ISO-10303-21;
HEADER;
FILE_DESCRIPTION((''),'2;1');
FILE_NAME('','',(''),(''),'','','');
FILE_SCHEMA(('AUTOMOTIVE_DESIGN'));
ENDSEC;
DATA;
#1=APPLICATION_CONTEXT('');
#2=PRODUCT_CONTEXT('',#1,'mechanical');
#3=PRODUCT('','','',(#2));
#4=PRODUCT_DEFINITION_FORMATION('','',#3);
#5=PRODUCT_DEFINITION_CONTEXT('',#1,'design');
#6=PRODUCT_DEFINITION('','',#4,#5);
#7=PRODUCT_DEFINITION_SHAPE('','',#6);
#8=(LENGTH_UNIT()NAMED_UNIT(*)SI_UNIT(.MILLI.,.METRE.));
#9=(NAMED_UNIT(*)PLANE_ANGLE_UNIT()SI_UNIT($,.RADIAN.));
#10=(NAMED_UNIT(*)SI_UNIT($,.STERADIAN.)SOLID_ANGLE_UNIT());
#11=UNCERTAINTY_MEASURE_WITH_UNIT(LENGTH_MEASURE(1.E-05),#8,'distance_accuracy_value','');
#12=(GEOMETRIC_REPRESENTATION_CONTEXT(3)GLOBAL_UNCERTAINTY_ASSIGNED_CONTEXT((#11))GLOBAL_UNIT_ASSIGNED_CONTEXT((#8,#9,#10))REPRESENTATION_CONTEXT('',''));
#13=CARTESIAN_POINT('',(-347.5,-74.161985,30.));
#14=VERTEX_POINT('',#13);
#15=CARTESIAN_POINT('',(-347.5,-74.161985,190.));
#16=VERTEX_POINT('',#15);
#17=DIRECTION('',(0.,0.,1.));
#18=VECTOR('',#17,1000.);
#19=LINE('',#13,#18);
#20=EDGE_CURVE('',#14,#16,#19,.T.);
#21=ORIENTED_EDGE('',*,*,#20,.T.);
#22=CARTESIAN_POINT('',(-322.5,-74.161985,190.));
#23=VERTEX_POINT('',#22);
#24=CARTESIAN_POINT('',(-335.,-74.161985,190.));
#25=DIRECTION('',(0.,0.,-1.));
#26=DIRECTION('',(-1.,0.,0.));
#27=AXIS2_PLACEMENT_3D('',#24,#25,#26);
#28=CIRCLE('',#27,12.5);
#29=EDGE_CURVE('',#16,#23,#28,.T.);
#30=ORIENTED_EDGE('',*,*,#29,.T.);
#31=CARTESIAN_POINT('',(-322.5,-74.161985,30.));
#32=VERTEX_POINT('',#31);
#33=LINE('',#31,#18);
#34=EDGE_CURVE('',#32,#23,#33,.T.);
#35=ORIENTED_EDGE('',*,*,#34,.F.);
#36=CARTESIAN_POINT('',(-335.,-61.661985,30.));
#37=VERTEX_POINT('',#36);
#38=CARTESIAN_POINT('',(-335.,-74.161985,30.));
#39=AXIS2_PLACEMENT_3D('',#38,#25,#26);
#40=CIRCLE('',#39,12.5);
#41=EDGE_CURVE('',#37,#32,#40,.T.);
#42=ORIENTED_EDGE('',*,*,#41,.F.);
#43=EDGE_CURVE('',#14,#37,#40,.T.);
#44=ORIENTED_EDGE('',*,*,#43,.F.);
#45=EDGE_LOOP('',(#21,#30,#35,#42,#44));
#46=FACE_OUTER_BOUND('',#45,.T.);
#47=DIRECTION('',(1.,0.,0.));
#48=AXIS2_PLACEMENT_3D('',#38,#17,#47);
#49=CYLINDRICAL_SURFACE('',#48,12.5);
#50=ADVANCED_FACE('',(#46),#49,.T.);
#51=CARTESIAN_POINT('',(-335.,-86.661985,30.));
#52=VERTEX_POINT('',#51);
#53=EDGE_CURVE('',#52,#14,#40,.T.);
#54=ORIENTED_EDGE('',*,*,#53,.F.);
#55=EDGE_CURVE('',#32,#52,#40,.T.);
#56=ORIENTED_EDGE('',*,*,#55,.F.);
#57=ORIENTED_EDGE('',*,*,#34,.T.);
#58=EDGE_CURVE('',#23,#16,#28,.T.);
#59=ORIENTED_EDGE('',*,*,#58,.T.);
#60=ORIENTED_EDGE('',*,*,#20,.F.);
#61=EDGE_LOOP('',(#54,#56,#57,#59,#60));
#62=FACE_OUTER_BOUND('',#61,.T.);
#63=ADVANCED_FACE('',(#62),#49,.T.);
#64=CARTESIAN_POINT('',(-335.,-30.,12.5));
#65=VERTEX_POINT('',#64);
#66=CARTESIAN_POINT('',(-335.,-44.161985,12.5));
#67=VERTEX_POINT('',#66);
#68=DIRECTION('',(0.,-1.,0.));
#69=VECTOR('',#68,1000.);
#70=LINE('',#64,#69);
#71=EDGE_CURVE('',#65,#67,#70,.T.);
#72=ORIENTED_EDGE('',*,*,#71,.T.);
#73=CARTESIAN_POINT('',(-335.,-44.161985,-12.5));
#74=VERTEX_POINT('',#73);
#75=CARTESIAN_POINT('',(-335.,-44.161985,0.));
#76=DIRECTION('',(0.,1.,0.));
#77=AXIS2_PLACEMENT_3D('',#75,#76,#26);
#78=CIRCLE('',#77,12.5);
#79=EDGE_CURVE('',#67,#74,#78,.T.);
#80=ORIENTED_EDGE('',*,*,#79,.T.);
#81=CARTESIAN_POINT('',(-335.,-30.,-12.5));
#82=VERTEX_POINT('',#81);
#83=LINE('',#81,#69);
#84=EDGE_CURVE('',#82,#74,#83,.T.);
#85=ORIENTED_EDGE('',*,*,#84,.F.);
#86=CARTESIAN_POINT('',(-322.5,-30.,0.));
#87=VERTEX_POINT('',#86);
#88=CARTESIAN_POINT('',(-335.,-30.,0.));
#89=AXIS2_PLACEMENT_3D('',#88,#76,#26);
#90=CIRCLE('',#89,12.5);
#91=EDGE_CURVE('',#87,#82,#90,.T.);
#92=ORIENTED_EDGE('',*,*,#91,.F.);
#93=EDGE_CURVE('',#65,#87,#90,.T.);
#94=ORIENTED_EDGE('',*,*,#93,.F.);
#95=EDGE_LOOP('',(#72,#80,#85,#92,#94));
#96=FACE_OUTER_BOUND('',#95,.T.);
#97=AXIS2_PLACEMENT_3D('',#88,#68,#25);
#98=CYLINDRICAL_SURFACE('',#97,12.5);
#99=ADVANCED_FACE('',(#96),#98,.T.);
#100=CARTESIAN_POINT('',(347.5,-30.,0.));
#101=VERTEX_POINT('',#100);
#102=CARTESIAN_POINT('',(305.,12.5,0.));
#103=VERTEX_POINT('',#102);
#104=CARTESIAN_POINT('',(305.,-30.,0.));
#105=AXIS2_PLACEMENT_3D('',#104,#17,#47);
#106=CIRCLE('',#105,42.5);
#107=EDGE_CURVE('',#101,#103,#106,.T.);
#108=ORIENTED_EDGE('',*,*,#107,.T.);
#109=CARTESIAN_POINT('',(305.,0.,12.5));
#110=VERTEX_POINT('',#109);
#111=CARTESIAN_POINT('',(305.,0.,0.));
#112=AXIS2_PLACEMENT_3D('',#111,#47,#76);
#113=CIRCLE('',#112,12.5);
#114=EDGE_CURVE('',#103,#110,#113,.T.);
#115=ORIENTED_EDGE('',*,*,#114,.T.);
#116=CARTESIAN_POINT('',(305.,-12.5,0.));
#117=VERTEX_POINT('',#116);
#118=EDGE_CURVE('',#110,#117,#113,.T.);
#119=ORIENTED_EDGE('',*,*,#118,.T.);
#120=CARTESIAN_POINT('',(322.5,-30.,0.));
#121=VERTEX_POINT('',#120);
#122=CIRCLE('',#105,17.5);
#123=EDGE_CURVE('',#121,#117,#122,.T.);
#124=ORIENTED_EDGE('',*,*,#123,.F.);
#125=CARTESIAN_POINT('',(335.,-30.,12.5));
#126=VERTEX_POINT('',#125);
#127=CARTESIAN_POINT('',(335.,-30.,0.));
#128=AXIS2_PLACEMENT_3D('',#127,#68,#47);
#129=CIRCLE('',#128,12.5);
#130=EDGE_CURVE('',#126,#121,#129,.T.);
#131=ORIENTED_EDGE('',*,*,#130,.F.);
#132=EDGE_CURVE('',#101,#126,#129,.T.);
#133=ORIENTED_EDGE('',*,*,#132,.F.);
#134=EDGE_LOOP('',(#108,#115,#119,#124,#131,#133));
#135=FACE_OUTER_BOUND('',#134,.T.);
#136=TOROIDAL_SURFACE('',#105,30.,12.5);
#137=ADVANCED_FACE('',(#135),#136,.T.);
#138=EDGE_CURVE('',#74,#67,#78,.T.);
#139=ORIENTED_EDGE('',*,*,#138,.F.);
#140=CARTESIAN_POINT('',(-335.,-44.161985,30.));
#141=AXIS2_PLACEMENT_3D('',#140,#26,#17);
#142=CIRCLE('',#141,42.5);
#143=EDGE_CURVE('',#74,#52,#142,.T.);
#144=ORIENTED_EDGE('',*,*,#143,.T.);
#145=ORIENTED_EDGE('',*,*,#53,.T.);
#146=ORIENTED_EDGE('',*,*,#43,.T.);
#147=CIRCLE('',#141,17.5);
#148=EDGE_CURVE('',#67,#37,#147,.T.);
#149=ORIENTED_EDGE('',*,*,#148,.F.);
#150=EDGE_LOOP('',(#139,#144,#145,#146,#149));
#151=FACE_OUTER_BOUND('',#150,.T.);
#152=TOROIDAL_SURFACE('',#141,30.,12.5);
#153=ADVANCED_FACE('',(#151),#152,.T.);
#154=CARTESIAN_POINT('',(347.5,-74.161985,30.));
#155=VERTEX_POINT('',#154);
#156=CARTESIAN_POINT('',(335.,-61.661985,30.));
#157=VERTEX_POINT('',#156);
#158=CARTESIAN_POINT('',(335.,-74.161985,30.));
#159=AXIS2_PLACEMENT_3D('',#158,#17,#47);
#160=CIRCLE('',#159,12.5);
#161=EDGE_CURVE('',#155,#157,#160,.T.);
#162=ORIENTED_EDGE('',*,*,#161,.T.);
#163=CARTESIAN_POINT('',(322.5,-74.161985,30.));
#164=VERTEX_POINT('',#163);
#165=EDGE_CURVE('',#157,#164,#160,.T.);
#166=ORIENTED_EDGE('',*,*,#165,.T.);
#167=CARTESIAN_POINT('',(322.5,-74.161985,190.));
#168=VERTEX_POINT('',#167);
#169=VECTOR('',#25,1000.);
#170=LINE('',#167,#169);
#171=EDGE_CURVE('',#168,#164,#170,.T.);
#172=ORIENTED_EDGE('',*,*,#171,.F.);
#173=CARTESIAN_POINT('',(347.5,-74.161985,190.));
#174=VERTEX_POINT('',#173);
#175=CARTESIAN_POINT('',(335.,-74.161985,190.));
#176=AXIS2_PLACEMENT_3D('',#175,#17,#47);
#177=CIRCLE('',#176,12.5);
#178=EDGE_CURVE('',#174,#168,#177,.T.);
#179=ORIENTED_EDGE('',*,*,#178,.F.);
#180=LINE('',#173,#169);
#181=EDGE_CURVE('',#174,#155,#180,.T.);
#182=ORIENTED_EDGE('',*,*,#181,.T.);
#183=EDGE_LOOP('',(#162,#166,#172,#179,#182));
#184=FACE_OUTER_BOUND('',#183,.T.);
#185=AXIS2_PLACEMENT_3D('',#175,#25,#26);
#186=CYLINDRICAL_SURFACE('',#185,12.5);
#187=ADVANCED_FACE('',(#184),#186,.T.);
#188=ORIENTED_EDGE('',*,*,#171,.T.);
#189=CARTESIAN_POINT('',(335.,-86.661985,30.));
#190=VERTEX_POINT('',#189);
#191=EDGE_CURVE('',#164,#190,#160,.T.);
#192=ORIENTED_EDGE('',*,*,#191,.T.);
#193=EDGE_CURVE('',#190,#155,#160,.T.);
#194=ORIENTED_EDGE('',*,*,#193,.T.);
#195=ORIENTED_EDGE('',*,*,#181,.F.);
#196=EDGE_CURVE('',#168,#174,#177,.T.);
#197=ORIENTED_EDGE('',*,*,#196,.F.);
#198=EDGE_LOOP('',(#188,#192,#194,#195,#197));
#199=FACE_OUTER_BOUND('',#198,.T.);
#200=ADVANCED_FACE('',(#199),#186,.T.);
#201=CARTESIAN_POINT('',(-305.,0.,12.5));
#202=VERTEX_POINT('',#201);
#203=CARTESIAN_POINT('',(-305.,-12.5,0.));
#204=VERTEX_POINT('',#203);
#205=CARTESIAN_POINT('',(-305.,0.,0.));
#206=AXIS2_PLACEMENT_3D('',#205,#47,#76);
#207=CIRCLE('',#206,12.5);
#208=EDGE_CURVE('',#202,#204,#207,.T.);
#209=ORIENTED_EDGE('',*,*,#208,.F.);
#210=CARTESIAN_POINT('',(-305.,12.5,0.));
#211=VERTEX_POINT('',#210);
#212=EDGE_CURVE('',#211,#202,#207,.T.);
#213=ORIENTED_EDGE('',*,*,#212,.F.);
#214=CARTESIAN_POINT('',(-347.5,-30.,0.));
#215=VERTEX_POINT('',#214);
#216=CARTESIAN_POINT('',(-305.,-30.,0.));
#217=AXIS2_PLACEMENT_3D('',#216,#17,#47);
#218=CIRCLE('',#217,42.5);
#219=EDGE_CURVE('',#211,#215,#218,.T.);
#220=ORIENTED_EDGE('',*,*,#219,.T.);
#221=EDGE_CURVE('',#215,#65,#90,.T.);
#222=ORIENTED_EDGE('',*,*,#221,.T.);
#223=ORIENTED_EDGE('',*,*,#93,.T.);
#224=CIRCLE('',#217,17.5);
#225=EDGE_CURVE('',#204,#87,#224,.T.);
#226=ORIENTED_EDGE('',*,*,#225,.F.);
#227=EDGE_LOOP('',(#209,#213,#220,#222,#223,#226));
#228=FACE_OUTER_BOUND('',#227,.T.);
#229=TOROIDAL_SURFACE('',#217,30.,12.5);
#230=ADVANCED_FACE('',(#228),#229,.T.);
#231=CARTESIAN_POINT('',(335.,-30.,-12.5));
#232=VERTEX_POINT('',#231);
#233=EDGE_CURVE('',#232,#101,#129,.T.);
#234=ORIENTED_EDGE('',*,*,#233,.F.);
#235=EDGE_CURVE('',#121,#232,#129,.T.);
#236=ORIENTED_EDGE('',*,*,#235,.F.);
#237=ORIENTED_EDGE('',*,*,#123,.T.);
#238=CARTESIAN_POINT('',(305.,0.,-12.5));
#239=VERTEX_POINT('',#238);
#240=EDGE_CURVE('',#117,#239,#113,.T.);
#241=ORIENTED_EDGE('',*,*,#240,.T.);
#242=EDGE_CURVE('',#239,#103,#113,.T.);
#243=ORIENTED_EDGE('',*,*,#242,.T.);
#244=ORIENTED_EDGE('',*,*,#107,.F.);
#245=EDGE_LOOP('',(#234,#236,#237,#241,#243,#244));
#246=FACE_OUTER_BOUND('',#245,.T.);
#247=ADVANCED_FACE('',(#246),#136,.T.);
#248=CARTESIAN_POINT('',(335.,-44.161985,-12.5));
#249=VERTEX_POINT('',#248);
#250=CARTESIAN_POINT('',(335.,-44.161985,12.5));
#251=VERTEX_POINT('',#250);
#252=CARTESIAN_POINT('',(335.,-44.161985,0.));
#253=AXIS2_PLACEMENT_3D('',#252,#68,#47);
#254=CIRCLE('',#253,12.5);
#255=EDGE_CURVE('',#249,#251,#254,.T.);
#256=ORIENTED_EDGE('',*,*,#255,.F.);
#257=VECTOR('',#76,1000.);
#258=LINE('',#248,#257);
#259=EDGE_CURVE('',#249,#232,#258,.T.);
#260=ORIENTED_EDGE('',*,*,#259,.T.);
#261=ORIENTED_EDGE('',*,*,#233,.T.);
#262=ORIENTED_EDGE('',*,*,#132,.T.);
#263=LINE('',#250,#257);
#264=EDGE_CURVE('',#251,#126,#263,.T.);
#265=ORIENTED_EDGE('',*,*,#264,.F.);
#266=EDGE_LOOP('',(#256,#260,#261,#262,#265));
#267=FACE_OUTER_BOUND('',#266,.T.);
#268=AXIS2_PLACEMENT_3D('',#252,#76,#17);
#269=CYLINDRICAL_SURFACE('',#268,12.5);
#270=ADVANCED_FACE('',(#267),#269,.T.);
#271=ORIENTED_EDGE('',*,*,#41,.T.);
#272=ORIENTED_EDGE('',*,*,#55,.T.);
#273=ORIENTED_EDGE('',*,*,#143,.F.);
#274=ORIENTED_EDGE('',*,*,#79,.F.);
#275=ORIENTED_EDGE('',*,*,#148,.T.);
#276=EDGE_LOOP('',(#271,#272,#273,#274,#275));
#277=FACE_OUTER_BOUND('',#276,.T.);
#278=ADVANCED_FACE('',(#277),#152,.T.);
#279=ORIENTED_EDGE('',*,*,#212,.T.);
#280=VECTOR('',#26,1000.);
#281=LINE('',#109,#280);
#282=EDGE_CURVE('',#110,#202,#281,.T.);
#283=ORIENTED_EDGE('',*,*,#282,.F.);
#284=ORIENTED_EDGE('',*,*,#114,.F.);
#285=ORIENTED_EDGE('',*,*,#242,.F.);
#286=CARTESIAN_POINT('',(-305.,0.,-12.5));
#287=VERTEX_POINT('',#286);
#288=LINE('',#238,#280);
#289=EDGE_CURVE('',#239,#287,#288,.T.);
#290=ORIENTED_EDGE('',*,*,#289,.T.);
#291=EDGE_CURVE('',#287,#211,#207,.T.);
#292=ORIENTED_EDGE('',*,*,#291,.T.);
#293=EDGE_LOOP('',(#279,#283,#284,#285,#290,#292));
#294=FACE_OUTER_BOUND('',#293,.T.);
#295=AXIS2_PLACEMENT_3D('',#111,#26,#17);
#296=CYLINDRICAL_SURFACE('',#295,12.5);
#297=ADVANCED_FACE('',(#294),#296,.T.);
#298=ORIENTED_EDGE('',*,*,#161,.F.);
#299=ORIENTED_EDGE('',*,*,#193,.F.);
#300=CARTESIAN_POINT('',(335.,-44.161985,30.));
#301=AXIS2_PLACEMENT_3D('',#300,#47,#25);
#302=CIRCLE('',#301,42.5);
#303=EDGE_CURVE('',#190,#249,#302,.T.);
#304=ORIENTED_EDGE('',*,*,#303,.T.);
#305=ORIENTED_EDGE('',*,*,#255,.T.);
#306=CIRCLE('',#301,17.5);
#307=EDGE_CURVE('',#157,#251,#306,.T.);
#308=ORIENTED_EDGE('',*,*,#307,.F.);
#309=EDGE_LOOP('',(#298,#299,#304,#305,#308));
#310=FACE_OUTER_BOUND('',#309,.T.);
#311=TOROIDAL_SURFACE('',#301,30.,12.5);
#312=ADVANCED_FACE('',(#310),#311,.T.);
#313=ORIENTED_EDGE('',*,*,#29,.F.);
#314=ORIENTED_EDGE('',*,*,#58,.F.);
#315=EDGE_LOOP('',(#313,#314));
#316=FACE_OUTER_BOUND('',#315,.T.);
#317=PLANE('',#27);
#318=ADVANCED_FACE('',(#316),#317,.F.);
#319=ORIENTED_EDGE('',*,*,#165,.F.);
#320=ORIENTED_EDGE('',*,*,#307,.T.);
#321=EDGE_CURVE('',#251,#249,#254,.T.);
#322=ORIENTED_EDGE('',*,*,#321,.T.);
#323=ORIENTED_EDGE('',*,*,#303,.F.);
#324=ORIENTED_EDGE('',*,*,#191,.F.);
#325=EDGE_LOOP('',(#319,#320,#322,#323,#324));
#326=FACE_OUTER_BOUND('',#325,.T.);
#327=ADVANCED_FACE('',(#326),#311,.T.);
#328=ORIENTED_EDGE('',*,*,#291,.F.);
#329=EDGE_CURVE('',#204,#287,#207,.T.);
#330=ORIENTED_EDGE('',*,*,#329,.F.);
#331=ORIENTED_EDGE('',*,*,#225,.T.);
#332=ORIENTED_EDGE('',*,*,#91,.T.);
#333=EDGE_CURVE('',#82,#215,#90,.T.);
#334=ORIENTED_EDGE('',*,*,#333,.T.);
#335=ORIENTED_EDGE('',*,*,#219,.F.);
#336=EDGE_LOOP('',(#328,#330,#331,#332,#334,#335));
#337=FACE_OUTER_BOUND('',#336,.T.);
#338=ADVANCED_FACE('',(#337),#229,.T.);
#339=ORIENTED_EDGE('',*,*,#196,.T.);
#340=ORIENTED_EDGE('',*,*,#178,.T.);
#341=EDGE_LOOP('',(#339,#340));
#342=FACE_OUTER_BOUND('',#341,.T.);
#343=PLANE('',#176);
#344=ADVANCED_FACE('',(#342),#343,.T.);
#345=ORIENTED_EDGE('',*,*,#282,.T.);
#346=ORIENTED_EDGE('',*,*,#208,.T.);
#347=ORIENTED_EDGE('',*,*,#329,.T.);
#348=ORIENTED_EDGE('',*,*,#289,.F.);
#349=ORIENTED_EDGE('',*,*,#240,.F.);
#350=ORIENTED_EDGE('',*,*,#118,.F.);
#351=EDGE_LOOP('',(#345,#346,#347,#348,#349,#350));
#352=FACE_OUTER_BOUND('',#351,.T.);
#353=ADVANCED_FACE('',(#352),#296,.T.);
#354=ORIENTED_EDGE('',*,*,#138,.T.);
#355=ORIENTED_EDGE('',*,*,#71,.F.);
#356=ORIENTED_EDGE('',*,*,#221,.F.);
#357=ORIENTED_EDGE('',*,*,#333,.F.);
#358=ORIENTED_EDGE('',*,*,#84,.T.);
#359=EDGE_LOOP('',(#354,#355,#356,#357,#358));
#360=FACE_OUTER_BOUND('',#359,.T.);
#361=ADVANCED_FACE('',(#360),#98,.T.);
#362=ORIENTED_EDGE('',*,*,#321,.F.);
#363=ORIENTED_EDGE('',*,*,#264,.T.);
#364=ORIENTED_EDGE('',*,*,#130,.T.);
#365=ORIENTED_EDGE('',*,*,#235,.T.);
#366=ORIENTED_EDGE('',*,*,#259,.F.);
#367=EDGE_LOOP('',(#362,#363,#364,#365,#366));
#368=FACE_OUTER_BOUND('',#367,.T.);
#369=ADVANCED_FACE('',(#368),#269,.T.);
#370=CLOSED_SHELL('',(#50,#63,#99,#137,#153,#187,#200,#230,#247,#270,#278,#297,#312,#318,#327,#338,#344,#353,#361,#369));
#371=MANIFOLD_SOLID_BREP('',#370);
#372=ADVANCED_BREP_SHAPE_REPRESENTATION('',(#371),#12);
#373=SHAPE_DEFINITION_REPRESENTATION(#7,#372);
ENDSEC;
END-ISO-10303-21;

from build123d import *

# Parameters (mm, degrees)
SWEEP1_PROFILE_R = 12.5


with BuildPart() as part:
    # Sweep1: sweep along a curve in space
    with BuildLine() as sweep1_path:
        Line((335, -74.161984871, 30), (335, -74.161984871, 190))
        ThreePointArc((335, -74.161984871, 30), (335, -65.375188307, 8.786796564), (335, -44.161984871, 0))
        Line((335, -30, 0), (335, -44.161984871, 0))
        ThreePointArc((335, -30, 0), (326.213203436, -8.786796564, 0), (305, 0, 0))
        Line((-305, 0, 0), (305, 0, 0))
        ThreePointArc((-305, 0, 0), (-326.213203436, -8.786796564, 0), (-335, -30, 0))
        Line((-335, -30, 0), (-335, -44.161984871, 0))
        ThreePointArc((-335, -74.161984871, 30), (-335, -65.375188307, 8.786796564), (-335, -44.161984871, 0))
        Line((-335, -74.161984871, 30), (-335, -74.161984871, 190))
    # Sweep1 profile (on start of the path) → Sweep1 (sweep)
    with BuildSketch(Plane(origin=(-335, -74.161984871, 190), x_dir=(-1, 0, 0), z_dir=(0, 0, -1))):
        Circle(SWEEP1_PROFILE_R)
    sweep(path=sweep1_path.line)


solid = part.part
